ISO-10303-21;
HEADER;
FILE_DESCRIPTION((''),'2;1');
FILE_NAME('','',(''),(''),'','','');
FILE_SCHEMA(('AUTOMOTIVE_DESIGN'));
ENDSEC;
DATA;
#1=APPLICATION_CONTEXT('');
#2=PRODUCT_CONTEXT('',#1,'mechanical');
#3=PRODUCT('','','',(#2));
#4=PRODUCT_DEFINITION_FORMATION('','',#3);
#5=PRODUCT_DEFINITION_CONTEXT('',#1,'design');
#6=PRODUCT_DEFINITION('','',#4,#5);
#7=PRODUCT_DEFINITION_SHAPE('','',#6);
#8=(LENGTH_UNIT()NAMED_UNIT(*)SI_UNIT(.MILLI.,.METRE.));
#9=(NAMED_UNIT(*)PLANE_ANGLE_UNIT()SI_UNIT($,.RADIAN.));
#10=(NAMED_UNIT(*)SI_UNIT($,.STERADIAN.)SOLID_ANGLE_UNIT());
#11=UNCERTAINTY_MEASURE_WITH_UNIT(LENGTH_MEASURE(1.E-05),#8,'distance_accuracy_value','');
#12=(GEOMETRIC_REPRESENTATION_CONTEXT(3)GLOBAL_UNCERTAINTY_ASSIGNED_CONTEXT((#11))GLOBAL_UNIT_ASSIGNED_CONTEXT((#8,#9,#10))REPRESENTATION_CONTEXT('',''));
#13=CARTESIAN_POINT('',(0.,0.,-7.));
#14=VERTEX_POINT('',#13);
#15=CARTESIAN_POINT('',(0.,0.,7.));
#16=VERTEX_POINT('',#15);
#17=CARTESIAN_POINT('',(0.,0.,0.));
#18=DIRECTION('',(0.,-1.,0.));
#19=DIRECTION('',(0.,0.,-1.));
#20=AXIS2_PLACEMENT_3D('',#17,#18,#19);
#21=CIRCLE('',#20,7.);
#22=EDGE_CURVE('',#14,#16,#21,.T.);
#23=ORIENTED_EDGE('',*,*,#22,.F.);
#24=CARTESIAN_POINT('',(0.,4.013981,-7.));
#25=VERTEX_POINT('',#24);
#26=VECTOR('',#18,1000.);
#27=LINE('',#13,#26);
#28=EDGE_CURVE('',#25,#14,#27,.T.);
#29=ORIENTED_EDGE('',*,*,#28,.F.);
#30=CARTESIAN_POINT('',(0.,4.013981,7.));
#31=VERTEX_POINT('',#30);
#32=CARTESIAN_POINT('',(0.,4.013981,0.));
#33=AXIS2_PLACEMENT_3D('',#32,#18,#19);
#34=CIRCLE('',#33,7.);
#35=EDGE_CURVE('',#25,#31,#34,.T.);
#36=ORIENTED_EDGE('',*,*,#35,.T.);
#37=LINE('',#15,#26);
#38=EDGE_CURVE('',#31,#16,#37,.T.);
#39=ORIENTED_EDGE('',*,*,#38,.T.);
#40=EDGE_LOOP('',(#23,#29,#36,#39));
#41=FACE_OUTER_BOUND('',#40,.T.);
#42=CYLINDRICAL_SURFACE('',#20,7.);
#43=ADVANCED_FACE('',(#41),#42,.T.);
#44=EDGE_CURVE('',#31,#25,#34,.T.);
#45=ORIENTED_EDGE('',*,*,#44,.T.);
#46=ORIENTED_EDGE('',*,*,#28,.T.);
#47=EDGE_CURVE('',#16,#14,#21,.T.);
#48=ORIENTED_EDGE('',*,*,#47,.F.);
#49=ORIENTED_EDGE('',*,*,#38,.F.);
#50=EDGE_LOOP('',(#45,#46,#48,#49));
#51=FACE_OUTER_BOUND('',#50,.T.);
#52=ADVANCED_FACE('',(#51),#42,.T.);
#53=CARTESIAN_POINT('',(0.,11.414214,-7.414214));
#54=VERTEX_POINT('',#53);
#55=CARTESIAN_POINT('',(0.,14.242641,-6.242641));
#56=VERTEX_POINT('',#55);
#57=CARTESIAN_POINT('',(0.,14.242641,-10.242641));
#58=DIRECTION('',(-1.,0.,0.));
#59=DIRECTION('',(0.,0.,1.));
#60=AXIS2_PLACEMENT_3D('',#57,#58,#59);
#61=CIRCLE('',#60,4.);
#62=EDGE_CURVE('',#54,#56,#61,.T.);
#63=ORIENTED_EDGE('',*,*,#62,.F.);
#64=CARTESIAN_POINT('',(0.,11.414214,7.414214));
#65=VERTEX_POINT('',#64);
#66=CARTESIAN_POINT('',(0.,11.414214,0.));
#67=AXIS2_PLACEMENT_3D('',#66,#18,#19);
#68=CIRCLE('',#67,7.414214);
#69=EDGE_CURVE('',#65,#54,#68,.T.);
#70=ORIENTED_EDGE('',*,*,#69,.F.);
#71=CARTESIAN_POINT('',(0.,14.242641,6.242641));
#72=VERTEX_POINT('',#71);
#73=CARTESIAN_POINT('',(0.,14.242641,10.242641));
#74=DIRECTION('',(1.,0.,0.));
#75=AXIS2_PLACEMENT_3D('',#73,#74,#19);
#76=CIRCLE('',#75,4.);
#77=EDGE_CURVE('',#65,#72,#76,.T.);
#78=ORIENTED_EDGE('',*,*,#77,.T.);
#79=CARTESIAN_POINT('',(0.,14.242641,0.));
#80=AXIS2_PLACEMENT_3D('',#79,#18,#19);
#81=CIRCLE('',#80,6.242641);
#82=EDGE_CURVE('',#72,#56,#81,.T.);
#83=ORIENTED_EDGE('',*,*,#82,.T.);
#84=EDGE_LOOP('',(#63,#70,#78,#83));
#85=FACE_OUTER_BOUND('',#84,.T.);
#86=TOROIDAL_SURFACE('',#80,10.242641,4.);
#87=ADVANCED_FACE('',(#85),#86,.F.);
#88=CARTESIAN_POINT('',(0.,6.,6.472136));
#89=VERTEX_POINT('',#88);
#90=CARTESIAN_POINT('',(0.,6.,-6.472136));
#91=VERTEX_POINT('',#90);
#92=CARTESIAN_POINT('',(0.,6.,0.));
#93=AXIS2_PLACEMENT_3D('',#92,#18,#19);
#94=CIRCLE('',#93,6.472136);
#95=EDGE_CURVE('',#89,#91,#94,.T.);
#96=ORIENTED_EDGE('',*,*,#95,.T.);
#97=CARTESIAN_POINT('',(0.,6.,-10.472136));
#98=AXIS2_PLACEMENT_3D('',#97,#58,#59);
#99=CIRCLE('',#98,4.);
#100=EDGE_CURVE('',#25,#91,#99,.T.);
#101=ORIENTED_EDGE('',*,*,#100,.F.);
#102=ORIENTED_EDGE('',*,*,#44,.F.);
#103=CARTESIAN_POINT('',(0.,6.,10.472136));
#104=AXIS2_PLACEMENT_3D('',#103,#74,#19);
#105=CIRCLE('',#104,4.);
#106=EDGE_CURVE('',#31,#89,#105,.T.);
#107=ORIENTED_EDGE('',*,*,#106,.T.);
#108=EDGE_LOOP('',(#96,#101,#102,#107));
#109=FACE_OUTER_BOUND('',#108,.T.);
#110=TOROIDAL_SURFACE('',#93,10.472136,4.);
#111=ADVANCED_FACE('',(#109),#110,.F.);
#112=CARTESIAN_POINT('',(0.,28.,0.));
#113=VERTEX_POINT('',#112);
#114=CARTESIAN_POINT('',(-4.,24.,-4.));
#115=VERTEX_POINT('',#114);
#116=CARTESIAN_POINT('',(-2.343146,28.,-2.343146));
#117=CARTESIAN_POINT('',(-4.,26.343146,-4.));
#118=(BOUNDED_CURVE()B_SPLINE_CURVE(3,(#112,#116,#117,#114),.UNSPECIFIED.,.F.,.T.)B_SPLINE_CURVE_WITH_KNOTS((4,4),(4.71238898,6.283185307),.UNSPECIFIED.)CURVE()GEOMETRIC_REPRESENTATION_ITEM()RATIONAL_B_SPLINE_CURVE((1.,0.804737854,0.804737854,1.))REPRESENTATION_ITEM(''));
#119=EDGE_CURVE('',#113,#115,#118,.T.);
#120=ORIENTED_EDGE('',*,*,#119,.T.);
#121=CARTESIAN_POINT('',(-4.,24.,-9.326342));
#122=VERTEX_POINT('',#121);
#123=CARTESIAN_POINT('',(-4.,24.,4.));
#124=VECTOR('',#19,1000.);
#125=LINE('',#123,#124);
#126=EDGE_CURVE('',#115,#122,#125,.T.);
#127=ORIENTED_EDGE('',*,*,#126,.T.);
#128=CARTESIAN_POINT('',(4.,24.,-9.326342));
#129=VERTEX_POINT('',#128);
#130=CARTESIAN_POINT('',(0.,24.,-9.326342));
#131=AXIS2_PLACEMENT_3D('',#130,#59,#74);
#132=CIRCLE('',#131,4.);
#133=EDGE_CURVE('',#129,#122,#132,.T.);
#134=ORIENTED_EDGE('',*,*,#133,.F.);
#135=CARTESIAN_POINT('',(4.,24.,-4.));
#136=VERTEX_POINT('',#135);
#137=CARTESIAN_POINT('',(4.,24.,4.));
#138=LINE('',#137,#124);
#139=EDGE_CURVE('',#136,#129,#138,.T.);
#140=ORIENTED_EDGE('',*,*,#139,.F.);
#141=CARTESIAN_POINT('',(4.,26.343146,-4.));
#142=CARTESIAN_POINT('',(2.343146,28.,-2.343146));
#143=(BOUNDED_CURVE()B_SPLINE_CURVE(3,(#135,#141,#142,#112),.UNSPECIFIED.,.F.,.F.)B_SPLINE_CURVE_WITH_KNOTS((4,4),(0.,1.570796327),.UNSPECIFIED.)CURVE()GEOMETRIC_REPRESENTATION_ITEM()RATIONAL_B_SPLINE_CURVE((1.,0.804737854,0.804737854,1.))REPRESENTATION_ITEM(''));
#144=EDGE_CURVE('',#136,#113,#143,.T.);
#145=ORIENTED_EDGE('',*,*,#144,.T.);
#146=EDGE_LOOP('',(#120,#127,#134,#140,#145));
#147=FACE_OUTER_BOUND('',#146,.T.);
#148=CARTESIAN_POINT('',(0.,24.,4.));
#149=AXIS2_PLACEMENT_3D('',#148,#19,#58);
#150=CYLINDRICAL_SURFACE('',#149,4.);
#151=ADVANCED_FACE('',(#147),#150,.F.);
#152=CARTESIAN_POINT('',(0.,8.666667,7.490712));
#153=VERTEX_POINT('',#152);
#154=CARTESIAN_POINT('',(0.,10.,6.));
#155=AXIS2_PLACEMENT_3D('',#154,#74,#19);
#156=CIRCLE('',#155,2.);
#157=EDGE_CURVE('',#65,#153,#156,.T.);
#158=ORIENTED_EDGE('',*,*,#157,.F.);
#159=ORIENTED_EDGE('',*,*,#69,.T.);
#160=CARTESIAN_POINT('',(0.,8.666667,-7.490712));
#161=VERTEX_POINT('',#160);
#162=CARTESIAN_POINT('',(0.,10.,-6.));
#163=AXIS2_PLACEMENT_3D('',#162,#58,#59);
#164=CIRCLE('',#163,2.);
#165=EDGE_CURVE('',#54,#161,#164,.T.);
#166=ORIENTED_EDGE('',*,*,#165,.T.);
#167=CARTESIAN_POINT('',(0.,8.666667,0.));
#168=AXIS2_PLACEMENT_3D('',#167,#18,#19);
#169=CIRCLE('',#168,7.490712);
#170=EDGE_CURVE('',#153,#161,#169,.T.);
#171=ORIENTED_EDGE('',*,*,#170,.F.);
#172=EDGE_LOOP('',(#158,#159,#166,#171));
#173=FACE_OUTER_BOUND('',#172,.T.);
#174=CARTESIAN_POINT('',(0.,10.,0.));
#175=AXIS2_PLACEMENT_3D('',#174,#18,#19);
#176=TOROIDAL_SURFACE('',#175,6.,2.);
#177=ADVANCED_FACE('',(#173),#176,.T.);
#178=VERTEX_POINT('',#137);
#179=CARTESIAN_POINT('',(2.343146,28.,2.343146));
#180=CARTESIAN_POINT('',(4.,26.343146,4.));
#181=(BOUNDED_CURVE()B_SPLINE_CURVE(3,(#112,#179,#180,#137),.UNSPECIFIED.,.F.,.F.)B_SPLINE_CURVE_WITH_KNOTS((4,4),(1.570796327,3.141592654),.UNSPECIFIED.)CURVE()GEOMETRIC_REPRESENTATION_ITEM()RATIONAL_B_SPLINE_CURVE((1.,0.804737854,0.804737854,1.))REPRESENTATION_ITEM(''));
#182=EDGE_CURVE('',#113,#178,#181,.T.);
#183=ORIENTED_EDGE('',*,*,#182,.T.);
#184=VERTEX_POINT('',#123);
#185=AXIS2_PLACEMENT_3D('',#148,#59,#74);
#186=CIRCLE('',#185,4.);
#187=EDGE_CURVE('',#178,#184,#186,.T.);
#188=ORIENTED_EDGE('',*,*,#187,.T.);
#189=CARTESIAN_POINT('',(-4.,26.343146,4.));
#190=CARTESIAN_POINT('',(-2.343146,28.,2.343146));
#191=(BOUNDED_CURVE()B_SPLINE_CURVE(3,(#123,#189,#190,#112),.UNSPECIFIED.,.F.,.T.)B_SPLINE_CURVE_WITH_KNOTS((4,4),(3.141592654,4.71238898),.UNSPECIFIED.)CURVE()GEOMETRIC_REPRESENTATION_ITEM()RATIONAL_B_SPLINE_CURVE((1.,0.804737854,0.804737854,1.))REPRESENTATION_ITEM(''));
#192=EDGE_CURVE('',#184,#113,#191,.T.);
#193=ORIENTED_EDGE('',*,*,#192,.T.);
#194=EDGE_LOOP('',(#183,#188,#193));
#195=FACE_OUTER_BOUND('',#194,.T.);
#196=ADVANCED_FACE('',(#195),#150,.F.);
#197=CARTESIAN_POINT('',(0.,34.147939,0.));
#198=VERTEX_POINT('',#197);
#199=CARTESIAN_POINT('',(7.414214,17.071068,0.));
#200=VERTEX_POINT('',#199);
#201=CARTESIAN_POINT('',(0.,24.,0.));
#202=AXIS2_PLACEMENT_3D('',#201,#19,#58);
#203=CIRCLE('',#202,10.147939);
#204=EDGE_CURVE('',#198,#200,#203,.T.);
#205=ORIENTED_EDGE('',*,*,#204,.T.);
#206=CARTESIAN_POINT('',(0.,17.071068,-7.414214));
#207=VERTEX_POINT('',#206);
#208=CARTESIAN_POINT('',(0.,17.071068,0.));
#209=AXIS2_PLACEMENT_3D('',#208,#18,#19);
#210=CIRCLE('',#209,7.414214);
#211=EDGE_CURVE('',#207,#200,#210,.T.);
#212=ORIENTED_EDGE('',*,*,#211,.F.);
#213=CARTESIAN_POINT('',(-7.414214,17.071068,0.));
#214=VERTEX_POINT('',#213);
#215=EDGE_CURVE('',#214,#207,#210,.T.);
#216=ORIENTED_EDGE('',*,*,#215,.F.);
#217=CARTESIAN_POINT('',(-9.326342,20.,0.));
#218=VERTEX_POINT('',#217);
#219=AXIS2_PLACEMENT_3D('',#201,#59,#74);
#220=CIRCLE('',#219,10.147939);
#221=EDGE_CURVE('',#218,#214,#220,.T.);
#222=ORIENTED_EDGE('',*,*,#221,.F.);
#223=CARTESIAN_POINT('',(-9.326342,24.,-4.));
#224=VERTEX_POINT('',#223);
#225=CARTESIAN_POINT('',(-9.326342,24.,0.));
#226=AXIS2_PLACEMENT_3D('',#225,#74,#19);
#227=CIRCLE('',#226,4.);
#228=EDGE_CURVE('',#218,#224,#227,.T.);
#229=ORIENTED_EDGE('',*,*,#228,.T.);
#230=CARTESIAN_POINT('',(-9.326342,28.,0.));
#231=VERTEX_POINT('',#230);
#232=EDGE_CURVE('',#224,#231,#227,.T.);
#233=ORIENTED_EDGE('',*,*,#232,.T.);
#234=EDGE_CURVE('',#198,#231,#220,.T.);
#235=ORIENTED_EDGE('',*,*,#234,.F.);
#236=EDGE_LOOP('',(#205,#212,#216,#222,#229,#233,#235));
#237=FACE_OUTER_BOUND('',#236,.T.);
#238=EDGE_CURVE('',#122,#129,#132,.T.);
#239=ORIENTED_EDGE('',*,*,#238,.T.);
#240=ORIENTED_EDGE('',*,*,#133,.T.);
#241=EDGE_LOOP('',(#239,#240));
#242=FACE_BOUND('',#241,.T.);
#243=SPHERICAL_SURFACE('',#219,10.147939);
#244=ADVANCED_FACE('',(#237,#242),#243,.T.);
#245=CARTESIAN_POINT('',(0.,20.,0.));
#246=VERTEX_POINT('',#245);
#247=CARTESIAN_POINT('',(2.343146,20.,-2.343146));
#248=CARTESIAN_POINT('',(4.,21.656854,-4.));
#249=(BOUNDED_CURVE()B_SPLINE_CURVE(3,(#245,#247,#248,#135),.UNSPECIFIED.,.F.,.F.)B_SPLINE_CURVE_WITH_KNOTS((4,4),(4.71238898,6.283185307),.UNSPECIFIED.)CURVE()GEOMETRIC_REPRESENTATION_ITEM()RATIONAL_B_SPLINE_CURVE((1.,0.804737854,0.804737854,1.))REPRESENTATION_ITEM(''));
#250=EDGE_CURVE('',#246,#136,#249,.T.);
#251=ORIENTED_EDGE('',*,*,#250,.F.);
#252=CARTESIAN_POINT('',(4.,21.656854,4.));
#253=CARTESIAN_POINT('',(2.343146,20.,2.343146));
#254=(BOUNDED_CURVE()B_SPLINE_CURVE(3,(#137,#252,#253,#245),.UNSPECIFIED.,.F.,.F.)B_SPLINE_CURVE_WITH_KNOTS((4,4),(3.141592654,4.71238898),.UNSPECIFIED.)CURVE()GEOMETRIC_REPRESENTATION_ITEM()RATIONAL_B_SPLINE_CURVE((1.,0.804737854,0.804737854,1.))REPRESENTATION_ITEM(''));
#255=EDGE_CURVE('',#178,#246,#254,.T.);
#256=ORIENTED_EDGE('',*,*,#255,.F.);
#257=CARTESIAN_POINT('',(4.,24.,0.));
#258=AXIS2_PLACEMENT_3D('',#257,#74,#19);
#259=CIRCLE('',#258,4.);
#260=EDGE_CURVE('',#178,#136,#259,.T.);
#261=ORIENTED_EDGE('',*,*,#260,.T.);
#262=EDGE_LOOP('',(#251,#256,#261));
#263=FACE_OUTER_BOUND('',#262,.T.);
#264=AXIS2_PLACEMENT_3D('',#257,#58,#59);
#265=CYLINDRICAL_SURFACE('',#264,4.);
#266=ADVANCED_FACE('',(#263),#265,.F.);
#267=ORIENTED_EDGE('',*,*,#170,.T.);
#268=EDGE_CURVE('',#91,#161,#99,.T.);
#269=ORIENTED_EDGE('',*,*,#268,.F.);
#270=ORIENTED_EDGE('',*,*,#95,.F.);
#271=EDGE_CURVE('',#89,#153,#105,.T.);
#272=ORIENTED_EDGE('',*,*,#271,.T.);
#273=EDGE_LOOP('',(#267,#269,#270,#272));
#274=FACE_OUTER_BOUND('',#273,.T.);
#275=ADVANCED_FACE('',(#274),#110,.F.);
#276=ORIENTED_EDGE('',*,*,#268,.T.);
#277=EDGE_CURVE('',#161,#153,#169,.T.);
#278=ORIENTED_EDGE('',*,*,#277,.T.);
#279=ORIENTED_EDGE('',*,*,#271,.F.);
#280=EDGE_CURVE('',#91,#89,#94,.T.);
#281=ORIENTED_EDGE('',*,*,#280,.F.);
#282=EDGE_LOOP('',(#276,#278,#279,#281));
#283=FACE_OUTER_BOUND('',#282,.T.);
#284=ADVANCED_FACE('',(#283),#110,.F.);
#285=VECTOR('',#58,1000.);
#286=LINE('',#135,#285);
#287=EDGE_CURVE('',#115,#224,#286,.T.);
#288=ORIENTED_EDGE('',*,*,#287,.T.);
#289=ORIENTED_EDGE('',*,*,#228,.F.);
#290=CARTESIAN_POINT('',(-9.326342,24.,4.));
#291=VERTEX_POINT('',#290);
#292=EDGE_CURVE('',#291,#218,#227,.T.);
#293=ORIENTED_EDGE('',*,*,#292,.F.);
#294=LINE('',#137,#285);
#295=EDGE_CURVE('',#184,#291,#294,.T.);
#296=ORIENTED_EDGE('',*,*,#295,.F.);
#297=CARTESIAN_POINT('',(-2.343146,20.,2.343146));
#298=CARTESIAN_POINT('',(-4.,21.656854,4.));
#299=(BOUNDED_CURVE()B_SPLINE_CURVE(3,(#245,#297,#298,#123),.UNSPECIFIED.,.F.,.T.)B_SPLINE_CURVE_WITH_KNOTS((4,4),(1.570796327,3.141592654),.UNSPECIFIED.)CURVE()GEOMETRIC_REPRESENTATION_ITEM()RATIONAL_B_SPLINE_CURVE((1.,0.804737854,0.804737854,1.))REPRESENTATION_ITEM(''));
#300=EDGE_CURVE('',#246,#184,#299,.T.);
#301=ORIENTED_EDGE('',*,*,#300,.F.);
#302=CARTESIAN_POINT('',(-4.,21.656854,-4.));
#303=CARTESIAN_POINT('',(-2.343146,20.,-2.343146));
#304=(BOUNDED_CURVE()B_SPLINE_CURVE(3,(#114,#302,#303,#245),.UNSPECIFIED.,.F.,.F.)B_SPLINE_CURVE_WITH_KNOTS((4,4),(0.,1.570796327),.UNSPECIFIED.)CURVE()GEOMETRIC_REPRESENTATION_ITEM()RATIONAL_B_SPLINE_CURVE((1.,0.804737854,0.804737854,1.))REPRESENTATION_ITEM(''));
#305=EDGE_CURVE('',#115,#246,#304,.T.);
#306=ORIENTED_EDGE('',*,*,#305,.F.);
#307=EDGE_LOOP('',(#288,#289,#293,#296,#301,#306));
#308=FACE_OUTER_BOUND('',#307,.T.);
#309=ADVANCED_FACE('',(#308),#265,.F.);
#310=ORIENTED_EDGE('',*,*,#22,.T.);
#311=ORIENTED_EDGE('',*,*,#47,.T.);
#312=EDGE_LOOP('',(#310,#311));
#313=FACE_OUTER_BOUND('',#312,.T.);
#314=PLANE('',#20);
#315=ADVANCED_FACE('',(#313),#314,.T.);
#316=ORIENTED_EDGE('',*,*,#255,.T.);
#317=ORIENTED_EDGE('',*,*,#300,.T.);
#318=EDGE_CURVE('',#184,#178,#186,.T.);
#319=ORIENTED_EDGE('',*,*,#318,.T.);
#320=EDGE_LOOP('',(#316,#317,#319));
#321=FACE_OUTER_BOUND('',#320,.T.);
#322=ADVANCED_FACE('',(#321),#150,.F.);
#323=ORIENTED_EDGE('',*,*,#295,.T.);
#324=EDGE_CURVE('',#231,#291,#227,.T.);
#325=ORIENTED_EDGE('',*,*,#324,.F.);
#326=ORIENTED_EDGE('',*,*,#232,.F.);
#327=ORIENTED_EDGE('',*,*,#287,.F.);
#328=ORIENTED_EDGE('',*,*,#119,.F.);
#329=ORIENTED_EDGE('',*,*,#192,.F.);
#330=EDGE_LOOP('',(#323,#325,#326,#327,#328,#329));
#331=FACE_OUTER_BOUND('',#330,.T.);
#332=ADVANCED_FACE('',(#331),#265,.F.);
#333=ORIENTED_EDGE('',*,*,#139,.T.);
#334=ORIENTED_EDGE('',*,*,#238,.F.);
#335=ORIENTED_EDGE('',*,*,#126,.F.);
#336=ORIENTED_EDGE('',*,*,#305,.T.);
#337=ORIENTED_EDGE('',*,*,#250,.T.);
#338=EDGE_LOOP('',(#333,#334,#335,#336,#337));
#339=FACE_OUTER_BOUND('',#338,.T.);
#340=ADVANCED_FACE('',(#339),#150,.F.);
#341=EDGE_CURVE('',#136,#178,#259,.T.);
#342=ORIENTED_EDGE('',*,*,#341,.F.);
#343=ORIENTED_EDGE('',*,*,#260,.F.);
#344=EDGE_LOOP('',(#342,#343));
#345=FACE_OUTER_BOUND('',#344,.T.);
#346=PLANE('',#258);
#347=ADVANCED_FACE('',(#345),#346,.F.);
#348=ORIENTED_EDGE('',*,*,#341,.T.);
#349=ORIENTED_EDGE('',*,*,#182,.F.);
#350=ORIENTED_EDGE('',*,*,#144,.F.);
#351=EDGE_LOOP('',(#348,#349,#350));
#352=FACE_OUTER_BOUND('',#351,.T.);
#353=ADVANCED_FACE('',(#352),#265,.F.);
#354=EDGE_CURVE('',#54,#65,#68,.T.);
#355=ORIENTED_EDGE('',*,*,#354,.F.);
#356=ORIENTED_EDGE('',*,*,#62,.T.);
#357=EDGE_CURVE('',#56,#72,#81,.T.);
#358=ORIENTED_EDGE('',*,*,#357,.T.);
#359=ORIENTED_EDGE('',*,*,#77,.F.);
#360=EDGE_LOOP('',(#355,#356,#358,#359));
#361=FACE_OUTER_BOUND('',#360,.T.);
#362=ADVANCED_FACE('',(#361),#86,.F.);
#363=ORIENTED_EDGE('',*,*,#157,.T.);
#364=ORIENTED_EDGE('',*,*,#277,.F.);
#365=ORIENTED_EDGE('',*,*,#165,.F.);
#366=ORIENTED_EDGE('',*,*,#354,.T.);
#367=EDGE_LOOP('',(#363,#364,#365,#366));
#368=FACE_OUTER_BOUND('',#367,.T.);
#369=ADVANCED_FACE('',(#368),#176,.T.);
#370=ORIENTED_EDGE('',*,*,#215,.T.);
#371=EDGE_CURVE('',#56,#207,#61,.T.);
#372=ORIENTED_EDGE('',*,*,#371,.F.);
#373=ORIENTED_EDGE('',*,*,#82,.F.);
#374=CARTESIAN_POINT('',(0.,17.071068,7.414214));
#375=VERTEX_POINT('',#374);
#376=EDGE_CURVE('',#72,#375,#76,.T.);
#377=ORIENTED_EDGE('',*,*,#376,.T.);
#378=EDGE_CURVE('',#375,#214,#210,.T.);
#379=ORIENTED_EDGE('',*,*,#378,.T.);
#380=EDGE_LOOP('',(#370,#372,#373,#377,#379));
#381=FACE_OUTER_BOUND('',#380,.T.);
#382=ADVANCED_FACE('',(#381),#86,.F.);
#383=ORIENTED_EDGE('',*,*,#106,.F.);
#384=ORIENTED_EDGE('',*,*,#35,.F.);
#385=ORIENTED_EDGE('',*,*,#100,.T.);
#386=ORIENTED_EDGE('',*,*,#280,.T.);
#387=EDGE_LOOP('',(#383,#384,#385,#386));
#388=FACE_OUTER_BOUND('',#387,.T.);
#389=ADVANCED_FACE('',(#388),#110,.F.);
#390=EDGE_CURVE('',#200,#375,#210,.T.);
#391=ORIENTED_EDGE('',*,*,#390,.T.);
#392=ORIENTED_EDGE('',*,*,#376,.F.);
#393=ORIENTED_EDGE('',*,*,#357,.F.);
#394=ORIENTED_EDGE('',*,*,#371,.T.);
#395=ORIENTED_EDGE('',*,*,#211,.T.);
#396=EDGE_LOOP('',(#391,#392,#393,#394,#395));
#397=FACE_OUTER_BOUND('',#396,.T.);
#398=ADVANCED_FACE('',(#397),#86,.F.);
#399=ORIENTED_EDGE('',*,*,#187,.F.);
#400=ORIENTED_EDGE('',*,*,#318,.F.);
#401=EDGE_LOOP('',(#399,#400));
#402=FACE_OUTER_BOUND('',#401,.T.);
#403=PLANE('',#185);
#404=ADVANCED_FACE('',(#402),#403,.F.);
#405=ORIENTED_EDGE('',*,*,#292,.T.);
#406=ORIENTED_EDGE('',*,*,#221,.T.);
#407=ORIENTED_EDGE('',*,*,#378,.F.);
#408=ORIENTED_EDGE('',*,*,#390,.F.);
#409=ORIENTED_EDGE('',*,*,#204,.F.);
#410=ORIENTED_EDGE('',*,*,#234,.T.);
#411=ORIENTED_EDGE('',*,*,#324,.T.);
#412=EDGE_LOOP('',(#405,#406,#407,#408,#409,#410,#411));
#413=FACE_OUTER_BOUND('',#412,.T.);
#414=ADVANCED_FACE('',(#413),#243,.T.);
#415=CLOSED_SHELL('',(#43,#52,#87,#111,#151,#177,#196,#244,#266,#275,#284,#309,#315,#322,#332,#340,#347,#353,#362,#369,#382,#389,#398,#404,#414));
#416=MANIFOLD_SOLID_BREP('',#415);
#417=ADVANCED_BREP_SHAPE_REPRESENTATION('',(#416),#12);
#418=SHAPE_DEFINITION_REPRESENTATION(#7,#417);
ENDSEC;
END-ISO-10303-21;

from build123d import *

# Parameters (mm, degrees)
SIDE_CUT_A_8_DEPTH      = 4
SIDE_CUT_A_8_DEPTH_BACK = 14
SIDE_CUT_A_8_SKETCH_R   = 4
SIDE_CUT_B_8_DEPTH      = 4
SIDE_CUT_B_8_DEPTH_BACK = 14
SIDE_CUT_B_8_SKETCH_R   = 4


with BuildPart() as part:
    # Knob Profile Sketch → Knob Body Revolve (revolve)
    with BuildSketch(Plane.XY, mode=Mode.PRIVATE) as knob_body_revolve_sk:
        with BuildLine():
            Line((0, 24), (0, 0))
            Line((0, 0), (7, 0))
            Line((7, 0), (7, 4.013980889))
            ThreePointArc((7, 4.013980889), (6.494199283, 6.419547181), (7.490711985, 8.666666667))
            ThreePointArc((7.490711985, 8.666666667), (7.999225249, 10.055663319), (7.414213562, 11.414213562))
            ThreePointArc((7.414213562, 11.414213562), (6.243817658, 14.14561297), (7.28036451, 16.930561789))
            ThreePointArc((7.28036451, 16.930561789), (7.34643685, 17.001626612), (7.414213562, 17.071067812))
            ThreePointArc((7.414213562, 17.071067812), (9.308465087, 28.041428182), (0, 34.147938905))
            Line((0, 34.147938905), (0, 24))
        make_face()
    revolve(knob_body_revolve_sk.sketch.rotate(Axis((0, 0, 0), (0, 1, 0)), 90), axis=Axis((0, 0, 0), (0, 1, 0)))

    # Side Cut A Ø8 Sketch → Side Cut A Ø8 (cut, two sides: drawn at the far end of the back side and taken through both)
    with BuildSketch(Plane.XY.offset(-SIDE_CUT_A_8_DEPTH_BACK)):
        with Locations((0, 24)):
            Circle(SIDE_CUT_A_8_SKETCH_R)
    extrude(amount=SIDE_CUT_A_8_DEPTH + SIDE_CUT_A_8_DEPTH_BACK, mode=Mode.SUBTRACT)

    # Side Cut B Ø8 Sketch → Side Cut B Ø8 (cut, two sides: drawn at the far end of the back side and taken through both)
    with BuildSketch(Plane(origin=(0, 0, 0), x_dir=(0, 0, -1), z_dir=(1, 0, 0)).offset(-SIDE_CUT_B_8_DEPTH_BACK)):
        with Locations(Location((0, 24, 0), (0, 0, 180))):
            Circle(SIDE_CUT_B_8_SKETCH_R)
    extrude(amount=SIDE_CUT_B_8_DEPTH + SIDE_CUT_B_8_DEPTH_BACK, mode=Mode.SUBTRACT)


solid = part.part
